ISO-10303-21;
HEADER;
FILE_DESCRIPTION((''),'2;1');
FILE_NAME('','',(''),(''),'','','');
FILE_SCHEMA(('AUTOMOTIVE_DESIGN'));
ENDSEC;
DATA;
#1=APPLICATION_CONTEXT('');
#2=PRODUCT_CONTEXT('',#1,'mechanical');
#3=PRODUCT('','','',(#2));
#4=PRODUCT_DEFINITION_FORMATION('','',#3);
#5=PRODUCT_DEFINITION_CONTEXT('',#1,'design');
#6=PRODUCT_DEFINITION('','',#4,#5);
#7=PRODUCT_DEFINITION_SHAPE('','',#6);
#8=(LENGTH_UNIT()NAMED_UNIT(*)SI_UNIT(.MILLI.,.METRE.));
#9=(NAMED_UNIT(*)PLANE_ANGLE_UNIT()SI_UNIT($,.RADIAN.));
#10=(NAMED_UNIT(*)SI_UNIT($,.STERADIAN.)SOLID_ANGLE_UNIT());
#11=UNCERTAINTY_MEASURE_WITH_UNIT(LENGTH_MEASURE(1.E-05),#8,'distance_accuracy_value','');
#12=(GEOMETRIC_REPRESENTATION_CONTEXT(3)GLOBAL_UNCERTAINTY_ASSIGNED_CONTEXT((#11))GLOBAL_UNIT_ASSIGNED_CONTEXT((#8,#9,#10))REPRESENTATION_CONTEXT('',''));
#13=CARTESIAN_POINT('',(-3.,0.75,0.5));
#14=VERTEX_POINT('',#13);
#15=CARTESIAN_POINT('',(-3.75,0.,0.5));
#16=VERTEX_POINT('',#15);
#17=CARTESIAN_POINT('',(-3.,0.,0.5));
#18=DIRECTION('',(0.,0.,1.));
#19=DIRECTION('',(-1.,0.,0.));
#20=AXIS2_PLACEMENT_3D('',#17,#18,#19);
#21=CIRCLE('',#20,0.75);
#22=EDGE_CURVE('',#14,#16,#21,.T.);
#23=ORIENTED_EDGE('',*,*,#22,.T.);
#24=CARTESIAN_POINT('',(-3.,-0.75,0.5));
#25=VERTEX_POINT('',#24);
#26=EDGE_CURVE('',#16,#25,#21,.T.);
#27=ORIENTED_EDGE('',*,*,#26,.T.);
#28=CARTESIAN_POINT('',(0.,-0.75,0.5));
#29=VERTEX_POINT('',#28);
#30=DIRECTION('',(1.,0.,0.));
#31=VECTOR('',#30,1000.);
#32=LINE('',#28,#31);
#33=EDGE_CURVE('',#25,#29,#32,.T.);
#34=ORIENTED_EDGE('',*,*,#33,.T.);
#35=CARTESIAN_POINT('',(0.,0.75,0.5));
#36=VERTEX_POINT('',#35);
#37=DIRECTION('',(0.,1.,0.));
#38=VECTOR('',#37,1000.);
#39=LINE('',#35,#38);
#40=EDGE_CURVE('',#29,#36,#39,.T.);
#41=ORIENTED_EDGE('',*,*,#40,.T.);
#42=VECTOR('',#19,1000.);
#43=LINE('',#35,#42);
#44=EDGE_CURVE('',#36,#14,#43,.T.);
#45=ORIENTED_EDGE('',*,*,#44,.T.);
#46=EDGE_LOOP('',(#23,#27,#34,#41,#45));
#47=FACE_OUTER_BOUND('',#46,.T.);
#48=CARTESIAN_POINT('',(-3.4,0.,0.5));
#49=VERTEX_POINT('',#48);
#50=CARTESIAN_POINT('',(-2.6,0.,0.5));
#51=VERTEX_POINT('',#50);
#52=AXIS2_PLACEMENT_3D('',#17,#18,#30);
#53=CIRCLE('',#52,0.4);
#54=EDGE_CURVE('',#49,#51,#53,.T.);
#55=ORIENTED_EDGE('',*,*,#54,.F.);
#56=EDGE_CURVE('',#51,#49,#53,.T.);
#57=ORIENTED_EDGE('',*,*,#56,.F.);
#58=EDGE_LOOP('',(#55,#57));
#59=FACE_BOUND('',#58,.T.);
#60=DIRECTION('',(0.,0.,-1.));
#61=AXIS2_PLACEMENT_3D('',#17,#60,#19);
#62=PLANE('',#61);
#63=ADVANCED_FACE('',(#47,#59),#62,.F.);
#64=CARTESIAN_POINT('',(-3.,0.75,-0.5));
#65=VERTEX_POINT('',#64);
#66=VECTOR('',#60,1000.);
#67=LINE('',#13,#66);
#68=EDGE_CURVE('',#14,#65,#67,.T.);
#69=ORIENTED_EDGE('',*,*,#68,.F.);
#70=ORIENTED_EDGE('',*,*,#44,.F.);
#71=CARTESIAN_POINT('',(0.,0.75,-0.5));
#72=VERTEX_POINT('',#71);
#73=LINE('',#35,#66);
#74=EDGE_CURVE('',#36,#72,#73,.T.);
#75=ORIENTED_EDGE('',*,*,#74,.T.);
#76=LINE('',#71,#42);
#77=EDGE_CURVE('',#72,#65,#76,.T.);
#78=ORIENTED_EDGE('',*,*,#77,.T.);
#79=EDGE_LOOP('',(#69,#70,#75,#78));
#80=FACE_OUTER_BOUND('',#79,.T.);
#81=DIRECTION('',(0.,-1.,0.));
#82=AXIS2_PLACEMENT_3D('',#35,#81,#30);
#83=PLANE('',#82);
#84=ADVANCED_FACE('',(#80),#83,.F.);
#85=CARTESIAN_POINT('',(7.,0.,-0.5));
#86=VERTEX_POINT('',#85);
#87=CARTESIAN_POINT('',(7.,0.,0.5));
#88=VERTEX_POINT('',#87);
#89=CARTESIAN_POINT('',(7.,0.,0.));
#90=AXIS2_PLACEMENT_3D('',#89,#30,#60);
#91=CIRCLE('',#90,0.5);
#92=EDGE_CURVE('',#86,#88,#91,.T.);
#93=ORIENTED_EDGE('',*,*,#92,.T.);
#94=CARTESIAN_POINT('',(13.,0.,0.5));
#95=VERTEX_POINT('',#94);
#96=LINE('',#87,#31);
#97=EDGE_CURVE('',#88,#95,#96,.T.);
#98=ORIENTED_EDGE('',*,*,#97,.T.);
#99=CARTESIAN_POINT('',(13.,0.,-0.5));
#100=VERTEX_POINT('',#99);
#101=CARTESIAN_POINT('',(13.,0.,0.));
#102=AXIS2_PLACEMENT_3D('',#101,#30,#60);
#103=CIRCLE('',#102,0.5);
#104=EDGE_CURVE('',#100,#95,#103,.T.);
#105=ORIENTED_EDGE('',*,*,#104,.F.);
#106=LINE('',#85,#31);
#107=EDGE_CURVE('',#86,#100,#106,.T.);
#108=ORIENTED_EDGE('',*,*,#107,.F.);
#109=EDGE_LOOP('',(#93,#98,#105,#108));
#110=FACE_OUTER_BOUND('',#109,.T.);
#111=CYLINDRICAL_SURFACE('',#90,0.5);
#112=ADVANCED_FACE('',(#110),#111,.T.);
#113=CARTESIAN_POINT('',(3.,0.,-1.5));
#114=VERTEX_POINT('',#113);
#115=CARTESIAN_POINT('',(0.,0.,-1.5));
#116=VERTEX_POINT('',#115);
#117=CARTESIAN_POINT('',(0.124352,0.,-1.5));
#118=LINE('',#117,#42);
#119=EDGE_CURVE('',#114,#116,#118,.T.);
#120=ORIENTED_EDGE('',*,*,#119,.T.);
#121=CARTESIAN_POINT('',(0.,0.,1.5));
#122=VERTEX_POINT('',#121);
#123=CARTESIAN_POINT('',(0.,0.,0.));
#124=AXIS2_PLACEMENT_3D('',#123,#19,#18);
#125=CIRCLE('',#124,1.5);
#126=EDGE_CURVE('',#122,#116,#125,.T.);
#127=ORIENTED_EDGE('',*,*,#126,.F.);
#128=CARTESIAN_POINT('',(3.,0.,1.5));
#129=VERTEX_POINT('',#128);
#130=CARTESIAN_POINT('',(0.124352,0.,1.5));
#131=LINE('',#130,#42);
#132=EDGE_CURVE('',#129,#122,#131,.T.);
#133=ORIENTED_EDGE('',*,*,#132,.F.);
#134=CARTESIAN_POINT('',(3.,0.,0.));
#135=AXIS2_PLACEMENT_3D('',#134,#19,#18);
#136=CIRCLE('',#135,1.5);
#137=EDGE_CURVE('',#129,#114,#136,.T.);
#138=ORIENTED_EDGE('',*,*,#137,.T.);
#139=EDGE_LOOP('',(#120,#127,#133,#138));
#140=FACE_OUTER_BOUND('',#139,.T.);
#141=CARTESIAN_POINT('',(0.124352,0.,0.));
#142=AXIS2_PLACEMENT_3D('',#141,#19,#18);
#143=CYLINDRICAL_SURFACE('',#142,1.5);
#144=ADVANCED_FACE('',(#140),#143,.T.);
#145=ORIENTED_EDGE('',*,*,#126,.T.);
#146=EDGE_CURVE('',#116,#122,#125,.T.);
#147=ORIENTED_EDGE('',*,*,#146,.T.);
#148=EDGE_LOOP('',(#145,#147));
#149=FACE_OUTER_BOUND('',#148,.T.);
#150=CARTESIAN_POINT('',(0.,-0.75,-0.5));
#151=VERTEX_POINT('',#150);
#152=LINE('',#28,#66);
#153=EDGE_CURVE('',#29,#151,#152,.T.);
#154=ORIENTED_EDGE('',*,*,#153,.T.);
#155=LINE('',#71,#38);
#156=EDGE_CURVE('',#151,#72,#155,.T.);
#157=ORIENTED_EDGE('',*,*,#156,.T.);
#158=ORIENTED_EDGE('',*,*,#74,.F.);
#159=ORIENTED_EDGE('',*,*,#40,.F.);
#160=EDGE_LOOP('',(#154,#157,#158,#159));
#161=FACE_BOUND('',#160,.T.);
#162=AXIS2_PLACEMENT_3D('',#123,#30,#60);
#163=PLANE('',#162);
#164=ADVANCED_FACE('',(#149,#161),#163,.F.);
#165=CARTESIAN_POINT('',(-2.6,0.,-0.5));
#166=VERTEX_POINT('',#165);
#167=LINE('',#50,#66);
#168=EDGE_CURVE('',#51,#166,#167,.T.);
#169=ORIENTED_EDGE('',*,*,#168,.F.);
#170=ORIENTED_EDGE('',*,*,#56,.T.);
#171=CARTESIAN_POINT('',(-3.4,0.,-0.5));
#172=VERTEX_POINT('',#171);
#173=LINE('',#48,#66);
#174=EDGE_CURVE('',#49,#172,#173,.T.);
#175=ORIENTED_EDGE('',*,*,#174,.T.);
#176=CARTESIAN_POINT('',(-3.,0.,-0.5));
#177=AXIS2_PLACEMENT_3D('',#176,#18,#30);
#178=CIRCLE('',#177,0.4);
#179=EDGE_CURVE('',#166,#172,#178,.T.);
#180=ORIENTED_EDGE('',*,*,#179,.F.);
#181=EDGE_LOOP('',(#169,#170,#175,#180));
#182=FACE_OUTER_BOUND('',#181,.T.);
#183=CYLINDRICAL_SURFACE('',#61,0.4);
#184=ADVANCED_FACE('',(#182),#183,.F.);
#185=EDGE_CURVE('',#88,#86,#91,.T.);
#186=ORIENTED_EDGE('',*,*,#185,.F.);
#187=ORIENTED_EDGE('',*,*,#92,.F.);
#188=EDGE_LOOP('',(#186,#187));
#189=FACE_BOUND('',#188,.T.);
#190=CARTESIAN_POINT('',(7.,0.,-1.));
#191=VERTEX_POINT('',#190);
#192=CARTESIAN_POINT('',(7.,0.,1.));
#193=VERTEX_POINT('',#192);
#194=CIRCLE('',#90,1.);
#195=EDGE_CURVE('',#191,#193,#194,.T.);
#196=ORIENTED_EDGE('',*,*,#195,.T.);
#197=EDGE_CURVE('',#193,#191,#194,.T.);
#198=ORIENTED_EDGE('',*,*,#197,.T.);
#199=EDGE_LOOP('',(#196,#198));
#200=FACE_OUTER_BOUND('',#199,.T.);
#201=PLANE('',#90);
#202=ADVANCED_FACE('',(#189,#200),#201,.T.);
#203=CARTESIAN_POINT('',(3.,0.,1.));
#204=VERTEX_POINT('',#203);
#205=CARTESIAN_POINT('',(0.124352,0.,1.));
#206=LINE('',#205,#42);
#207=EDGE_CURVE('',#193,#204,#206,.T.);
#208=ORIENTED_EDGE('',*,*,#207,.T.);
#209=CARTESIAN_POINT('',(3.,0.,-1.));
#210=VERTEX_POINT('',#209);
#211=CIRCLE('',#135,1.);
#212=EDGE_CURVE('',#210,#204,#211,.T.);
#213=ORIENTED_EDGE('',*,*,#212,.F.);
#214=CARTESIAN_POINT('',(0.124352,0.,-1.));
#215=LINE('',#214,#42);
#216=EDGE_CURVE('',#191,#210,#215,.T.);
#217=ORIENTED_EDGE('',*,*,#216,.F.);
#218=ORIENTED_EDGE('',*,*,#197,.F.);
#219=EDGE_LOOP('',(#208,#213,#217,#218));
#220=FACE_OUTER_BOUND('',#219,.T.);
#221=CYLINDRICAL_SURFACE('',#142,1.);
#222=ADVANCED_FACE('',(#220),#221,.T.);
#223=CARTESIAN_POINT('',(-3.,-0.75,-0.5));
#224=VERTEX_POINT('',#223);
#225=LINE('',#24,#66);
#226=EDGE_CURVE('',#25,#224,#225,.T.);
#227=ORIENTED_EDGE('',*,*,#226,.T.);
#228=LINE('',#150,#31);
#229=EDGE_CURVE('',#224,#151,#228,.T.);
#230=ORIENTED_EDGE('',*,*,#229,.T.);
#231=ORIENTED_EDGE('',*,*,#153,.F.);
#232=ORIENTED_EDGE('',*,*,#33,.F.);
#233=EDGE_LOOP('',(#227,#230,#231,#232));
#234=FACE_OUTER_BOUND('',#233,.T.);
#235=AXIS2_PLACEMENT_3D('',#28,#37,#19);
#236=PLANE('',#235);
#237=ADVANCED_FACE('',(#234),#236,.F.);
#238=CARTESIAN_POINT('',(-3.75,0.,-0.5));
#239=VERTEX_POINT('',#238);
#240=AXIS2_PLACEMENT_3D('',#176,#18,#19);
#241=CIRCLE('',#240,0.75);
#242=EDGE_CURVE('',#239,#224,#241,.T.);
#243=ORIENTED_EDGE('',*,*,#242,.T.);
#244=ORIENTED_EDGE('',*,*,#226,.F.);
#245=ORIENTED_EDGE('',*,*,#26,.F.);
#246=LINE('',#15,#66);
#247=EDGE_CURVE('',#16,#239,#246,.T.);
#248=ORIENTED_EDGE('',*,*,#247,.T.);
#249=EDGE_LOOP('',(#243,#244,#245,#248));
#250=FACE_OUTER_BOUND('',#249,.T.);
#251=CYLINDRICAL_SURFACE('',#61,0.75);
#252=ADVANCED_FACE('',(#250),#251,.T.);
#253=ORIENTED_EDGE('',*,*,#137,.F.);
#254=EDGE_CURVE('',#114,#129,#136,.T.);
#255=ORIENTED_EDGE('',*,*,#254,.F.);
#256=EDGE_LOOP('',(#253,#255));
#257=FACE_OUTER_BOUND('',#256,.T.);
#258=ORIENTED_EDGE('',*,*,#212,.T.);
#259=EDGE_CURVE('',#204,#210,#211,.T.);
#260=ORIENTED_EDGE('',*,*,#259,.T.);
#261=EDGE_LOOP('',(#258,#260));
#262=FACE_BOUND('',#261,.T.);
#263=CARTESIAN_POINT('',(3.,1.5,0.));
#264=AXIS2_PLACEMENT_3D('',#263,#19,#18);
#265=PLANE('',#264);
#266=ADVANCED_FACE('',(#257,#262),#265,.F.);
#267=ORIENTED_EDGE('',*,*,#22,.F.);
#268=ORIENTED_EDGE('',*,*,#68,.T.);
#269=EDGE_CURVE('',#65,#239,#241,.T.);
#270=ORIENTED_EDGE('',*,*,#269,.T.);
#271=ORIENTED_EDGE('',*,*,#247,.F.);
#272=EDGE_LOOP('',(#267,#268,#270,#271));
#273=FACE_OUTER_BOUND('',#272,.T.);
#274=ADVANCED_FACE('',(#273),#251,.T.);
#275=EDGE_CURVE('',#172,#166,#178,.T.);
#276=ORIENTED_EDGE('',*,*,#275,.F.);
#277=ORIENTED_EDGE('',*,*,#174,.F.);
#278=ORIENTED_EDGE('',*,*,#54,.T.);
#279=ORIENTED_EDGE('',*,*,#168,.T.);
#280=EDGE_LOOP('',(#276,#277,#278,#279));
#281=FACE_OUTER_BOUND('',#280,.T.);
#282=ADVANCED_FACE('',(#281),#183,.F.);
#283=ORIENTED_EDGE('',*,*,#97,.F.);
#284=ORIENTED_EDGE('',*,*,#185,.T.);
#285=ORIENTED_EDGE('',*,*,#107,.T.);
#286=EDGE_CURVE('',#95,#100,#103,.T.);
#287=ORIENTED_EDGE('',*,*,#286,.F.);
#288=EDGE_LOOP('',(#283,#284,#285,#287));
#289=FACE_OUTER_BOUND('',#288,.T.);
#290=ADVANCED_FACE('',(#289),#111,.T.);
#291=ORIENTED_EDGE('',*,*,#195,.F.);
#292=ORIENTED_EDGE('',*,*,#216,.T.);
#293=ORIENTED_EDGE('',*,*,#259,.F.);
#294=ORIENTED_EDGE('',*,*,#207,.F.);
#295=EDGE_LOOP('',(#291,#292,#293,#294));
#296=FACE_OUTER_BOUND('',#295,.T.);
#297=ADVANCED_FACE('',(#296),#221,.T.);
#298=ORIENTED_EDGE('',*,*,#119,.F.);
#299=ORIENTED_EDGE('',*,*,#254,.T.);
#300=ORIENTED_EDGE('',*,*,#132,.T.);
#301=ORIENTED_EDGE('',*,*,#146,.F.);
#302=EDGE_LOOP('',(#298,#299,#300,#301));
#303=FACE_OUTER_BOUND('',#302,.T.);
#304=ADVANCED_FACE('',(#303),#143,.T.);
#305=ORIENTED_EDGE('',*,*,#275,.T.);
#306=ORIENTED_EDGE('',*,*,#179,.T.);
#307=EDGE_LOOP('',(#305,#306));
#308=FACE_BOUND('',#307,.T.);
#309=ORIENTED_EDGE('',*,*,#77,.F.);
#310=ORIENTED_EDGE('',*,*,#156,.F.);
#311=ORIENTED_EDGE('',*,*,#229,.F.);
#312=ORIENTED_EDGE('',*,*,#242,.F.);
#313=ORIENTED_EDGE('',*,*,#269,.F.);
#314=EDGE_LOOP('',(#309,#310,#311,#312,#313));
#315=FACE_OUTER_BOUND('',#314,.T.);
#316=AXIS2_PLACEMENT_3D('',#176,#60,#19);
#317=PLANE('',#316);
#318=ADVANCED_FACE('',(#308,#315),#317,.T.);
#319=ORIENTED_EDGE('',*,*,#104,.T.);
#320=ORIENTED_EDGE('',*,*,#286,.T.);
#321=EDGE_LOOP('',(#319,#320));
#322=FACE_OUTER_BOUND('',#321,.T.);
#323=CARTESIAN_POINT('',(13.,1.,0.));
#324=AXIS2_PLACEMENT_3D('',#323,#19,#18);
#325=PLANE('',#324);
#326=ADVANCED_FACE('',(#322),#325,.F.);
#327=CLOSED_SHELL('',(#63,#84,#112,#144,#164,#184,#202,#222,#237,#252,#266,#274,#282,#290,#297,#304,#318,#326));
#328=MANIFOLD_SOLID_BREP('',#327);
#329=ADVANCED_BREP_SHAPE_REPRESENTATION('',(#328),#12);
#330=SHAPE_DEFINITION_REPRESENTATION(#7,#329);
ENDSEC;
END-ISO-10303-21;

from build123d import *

# Parameters (mm, degrees)
SKETCH2_R           = 0.4
BOSS_EXTRUDE1_DEPTH = 0.5
SKETCH4_R           = 1
SKETCH4_R_2         = 0.5
CUT_EXTRUDE3_DEPTH  = 6


with BuildPart() as part:
    # Sketch1 → Revolve1 (revolve)
    with BuildSketch(Plane.XY, mode=Mode.PRIVATE) as revolve1_sk:
        Polygon((0, 0), (0, 1.5), (3, 1.5), (3, 1), (13, 1), (13, 0), align=None)
    revolve(revolve1_sk.sketch.rotate(Axis((0.124352332, 0, 0), (1, 0, 0)), 90), axis=Axis((0.124352332, 0, 0), (1, 0, 0)))

    # Sketch2 → Boss-Extrude1 (add, symmetric)
    with BuildSketch(Plane.XY):
        with BuildLine():
            Line((0, 0.75), (0, -0.75))
            Line((0, -0.75), (-3, -0.75))
            ThreePointArc((-3, -0.75), (-3.75, 0), (-3, 0.75))
            Line((-3, 0.75), (0, 0.75))
        make_face()
        with Locations((-3, 0)):
            Circle(SKETCH2_R, mode=Mode.SUBTRACT)
    extrude(amount=BOSS_EXTRUDE1_DEPTH, both=True)

    # Sketch4 → Cut-Extrude3 (cut)
    with BuildSketch(Plane(origin=(13, 0, 0), x_dir=(0, 0, -1), z_dir=(1, 0, 0))):
        with Locations(Location((0, 0, 0), (0, 0, 180))):
            Circle(SKETCH4_R)
        Circle(SKETCH4_R_2, mode=Mode.SUBTRACT)
    extrude(amount=-CUT_EXTRUDE3_DEPTH, mode=Mode.SUBTRACT)


solid = part.part
